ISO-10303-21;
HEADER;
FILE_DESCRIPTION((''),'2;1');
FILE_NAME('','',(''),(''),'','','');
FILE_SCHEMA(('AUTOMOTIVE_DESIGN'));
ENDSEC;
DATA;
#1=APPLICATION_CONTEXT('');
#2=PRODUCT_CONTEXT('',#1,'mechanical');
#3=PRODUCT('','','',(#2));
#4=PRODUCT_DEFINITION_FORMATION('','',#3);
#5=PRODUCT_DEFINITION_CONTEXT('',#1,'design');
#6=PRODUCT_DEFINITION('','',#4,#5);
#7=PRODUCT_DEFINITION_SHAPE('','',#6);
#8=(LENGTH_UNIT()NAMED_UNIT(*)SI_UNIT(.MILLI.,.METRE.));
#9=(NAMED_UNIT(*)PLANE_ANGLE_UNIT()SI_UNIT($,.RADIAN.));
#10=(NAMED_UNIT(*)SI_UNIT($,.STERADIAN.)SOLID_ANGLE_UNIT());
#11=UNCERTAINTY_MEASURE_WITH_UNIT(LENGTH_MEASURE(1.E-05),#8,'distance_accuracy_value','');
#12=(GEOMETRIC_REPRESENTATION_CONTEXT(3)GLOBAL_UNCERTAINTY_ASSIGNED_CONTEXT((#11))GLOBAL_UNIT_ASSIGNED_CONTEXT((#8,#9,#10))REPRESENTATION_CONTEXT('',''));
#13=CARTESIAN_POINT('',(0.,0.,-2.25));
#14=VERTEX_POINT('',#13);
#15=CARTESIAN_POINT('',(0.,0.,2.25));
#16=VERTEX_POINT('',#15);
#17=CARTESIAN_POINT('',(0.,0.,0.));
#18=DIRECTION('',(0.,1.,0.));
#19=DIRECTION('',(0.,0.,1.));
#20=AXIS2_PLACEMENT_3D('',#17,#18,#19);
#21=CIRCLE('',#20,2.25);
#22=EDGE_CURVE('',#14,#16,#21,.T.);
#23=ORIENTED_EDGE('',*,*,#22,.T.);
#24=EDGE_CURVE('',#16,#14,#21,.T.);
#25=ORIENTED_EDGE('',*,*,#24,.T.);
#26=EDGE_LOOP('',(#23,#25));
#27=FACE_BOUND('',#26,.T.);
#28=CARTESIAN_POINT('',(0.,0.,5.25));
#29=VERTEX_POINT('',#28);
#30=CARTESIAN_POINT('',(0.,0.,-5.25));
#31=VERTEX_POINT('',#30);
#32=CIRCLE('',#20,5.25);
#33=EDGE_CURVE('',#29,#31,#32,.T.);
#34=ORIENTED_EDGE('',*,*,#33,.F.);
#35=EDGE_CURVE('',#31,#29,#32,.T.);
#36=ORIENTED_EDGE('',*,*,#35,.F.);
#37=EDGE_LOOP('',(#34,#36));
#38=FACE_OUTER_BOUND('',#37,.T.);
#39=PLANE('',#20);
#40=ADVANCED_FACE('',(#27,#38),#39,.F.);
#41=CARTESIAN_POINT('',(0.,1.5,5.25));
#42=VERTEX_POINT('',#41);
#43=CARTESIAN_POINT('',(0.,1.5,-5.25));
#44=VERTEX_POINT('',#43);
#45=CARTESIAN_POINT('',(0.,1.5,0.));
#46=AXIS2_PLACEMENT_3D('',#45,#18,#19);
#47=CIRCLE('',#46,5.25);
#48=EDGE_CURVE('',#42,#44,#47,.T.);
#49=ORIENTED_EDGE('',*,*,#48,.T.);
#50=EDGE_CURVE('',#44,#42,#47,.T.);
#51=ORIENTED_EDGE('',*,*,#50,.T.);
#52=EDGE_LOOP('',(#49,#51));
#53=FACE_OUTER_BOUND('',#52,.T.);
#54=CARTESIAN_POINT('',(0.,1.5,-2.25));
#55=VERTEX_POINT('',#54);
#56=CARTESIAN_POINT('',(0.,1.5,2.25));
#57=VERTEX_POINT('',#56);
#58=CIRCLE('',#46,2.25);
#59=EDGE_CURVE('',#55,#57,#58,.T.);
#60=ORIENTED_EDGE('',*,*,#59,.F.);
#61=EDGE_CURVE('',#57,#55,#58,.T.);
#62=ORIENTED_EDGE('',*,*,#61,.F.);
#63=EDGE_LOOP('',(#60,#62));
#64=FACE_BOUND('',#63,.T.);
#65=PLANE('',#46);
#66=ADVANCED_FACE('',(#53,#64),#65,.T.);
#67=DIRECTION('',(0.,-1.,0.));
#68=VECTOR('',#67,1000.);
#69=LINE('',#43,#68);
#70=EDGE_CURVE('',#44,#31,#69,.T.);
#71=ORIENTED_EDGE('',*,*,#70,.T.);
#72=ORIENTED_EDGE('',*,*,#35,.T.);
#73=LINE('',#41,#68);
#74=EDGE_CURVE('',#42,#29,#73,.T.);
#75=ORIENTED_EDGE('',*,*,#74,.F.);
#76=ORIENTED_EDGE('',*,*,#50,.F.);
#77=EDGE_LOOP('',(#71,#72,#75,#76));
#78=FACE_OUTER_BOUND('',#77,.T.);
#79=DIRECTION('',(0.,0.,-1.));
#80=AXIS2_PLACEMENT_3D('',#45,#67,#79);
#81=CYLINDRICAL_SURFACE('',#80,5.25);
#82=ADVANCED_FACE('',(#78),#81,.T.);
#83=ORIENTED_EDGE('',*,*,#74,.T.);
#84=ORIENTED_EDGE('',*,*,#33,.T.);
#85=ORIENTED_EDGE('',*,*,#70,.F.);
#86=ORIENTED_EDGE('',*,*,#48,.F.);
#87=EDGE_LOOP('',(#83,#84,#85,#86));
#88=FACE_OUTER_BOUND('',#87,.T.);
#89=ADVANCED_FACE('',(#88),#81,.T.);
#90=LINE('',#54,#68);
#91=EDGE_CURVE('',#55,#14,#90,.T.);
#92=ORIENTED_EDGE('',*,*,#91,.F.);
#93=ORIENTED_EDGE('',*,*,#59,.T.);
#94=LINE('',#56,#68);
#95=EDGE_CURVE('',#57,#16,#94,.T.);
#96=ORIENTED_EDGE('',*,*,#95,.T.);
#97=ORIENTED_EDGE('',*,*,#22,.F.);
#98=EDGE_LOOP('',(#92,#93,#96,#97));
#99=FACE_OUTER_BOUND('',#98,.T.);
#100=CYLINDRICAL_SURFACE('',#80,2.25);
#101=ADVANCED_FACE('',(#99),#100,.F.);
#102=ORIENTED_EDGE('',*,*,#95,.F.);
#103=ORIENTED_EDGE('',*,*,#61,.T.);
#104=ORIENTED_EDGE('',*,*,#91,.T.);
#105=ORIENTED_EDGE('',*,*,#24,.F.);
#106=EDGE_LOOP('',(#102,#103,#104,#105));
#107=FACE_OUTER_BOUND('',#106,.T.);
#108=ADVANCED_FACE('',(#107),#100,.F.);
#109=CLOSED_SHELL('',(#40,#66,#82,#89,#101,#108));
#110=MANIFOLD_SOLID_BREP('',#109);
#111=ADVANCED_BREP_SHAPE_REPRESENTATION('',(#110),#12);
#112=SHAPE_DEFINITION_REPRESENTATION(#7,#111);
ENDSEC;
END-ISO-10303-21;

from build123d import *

# Parameters (mm, degrees)
SKETCH1_R           = 5.25
SKETCH1_R_2         = 2.25
BOSS_EXTRUDE1_DEPTH = 1.5


with BuildPart() as part:
    # Sketch1 → Boss-Extrude1 (new body)
    with BuildSketch(Plane(origin=(0, 0, 0), x_dir=(1, 0, 0), z_dir=(0, 1, 0))):
        with Locations(Location((0, 0, 0), (0, 0, 270))):
            Circle(SKETCH1_R)
        with Locations(Location((0, 0, 0), (0, 0, 270))):
            Circle(SKETCH1_R_2, mode=Mode.SUBTRACT)
    extrude(amount=BOSS_EXTRUDE1_DEPTH)


solid = part.part
